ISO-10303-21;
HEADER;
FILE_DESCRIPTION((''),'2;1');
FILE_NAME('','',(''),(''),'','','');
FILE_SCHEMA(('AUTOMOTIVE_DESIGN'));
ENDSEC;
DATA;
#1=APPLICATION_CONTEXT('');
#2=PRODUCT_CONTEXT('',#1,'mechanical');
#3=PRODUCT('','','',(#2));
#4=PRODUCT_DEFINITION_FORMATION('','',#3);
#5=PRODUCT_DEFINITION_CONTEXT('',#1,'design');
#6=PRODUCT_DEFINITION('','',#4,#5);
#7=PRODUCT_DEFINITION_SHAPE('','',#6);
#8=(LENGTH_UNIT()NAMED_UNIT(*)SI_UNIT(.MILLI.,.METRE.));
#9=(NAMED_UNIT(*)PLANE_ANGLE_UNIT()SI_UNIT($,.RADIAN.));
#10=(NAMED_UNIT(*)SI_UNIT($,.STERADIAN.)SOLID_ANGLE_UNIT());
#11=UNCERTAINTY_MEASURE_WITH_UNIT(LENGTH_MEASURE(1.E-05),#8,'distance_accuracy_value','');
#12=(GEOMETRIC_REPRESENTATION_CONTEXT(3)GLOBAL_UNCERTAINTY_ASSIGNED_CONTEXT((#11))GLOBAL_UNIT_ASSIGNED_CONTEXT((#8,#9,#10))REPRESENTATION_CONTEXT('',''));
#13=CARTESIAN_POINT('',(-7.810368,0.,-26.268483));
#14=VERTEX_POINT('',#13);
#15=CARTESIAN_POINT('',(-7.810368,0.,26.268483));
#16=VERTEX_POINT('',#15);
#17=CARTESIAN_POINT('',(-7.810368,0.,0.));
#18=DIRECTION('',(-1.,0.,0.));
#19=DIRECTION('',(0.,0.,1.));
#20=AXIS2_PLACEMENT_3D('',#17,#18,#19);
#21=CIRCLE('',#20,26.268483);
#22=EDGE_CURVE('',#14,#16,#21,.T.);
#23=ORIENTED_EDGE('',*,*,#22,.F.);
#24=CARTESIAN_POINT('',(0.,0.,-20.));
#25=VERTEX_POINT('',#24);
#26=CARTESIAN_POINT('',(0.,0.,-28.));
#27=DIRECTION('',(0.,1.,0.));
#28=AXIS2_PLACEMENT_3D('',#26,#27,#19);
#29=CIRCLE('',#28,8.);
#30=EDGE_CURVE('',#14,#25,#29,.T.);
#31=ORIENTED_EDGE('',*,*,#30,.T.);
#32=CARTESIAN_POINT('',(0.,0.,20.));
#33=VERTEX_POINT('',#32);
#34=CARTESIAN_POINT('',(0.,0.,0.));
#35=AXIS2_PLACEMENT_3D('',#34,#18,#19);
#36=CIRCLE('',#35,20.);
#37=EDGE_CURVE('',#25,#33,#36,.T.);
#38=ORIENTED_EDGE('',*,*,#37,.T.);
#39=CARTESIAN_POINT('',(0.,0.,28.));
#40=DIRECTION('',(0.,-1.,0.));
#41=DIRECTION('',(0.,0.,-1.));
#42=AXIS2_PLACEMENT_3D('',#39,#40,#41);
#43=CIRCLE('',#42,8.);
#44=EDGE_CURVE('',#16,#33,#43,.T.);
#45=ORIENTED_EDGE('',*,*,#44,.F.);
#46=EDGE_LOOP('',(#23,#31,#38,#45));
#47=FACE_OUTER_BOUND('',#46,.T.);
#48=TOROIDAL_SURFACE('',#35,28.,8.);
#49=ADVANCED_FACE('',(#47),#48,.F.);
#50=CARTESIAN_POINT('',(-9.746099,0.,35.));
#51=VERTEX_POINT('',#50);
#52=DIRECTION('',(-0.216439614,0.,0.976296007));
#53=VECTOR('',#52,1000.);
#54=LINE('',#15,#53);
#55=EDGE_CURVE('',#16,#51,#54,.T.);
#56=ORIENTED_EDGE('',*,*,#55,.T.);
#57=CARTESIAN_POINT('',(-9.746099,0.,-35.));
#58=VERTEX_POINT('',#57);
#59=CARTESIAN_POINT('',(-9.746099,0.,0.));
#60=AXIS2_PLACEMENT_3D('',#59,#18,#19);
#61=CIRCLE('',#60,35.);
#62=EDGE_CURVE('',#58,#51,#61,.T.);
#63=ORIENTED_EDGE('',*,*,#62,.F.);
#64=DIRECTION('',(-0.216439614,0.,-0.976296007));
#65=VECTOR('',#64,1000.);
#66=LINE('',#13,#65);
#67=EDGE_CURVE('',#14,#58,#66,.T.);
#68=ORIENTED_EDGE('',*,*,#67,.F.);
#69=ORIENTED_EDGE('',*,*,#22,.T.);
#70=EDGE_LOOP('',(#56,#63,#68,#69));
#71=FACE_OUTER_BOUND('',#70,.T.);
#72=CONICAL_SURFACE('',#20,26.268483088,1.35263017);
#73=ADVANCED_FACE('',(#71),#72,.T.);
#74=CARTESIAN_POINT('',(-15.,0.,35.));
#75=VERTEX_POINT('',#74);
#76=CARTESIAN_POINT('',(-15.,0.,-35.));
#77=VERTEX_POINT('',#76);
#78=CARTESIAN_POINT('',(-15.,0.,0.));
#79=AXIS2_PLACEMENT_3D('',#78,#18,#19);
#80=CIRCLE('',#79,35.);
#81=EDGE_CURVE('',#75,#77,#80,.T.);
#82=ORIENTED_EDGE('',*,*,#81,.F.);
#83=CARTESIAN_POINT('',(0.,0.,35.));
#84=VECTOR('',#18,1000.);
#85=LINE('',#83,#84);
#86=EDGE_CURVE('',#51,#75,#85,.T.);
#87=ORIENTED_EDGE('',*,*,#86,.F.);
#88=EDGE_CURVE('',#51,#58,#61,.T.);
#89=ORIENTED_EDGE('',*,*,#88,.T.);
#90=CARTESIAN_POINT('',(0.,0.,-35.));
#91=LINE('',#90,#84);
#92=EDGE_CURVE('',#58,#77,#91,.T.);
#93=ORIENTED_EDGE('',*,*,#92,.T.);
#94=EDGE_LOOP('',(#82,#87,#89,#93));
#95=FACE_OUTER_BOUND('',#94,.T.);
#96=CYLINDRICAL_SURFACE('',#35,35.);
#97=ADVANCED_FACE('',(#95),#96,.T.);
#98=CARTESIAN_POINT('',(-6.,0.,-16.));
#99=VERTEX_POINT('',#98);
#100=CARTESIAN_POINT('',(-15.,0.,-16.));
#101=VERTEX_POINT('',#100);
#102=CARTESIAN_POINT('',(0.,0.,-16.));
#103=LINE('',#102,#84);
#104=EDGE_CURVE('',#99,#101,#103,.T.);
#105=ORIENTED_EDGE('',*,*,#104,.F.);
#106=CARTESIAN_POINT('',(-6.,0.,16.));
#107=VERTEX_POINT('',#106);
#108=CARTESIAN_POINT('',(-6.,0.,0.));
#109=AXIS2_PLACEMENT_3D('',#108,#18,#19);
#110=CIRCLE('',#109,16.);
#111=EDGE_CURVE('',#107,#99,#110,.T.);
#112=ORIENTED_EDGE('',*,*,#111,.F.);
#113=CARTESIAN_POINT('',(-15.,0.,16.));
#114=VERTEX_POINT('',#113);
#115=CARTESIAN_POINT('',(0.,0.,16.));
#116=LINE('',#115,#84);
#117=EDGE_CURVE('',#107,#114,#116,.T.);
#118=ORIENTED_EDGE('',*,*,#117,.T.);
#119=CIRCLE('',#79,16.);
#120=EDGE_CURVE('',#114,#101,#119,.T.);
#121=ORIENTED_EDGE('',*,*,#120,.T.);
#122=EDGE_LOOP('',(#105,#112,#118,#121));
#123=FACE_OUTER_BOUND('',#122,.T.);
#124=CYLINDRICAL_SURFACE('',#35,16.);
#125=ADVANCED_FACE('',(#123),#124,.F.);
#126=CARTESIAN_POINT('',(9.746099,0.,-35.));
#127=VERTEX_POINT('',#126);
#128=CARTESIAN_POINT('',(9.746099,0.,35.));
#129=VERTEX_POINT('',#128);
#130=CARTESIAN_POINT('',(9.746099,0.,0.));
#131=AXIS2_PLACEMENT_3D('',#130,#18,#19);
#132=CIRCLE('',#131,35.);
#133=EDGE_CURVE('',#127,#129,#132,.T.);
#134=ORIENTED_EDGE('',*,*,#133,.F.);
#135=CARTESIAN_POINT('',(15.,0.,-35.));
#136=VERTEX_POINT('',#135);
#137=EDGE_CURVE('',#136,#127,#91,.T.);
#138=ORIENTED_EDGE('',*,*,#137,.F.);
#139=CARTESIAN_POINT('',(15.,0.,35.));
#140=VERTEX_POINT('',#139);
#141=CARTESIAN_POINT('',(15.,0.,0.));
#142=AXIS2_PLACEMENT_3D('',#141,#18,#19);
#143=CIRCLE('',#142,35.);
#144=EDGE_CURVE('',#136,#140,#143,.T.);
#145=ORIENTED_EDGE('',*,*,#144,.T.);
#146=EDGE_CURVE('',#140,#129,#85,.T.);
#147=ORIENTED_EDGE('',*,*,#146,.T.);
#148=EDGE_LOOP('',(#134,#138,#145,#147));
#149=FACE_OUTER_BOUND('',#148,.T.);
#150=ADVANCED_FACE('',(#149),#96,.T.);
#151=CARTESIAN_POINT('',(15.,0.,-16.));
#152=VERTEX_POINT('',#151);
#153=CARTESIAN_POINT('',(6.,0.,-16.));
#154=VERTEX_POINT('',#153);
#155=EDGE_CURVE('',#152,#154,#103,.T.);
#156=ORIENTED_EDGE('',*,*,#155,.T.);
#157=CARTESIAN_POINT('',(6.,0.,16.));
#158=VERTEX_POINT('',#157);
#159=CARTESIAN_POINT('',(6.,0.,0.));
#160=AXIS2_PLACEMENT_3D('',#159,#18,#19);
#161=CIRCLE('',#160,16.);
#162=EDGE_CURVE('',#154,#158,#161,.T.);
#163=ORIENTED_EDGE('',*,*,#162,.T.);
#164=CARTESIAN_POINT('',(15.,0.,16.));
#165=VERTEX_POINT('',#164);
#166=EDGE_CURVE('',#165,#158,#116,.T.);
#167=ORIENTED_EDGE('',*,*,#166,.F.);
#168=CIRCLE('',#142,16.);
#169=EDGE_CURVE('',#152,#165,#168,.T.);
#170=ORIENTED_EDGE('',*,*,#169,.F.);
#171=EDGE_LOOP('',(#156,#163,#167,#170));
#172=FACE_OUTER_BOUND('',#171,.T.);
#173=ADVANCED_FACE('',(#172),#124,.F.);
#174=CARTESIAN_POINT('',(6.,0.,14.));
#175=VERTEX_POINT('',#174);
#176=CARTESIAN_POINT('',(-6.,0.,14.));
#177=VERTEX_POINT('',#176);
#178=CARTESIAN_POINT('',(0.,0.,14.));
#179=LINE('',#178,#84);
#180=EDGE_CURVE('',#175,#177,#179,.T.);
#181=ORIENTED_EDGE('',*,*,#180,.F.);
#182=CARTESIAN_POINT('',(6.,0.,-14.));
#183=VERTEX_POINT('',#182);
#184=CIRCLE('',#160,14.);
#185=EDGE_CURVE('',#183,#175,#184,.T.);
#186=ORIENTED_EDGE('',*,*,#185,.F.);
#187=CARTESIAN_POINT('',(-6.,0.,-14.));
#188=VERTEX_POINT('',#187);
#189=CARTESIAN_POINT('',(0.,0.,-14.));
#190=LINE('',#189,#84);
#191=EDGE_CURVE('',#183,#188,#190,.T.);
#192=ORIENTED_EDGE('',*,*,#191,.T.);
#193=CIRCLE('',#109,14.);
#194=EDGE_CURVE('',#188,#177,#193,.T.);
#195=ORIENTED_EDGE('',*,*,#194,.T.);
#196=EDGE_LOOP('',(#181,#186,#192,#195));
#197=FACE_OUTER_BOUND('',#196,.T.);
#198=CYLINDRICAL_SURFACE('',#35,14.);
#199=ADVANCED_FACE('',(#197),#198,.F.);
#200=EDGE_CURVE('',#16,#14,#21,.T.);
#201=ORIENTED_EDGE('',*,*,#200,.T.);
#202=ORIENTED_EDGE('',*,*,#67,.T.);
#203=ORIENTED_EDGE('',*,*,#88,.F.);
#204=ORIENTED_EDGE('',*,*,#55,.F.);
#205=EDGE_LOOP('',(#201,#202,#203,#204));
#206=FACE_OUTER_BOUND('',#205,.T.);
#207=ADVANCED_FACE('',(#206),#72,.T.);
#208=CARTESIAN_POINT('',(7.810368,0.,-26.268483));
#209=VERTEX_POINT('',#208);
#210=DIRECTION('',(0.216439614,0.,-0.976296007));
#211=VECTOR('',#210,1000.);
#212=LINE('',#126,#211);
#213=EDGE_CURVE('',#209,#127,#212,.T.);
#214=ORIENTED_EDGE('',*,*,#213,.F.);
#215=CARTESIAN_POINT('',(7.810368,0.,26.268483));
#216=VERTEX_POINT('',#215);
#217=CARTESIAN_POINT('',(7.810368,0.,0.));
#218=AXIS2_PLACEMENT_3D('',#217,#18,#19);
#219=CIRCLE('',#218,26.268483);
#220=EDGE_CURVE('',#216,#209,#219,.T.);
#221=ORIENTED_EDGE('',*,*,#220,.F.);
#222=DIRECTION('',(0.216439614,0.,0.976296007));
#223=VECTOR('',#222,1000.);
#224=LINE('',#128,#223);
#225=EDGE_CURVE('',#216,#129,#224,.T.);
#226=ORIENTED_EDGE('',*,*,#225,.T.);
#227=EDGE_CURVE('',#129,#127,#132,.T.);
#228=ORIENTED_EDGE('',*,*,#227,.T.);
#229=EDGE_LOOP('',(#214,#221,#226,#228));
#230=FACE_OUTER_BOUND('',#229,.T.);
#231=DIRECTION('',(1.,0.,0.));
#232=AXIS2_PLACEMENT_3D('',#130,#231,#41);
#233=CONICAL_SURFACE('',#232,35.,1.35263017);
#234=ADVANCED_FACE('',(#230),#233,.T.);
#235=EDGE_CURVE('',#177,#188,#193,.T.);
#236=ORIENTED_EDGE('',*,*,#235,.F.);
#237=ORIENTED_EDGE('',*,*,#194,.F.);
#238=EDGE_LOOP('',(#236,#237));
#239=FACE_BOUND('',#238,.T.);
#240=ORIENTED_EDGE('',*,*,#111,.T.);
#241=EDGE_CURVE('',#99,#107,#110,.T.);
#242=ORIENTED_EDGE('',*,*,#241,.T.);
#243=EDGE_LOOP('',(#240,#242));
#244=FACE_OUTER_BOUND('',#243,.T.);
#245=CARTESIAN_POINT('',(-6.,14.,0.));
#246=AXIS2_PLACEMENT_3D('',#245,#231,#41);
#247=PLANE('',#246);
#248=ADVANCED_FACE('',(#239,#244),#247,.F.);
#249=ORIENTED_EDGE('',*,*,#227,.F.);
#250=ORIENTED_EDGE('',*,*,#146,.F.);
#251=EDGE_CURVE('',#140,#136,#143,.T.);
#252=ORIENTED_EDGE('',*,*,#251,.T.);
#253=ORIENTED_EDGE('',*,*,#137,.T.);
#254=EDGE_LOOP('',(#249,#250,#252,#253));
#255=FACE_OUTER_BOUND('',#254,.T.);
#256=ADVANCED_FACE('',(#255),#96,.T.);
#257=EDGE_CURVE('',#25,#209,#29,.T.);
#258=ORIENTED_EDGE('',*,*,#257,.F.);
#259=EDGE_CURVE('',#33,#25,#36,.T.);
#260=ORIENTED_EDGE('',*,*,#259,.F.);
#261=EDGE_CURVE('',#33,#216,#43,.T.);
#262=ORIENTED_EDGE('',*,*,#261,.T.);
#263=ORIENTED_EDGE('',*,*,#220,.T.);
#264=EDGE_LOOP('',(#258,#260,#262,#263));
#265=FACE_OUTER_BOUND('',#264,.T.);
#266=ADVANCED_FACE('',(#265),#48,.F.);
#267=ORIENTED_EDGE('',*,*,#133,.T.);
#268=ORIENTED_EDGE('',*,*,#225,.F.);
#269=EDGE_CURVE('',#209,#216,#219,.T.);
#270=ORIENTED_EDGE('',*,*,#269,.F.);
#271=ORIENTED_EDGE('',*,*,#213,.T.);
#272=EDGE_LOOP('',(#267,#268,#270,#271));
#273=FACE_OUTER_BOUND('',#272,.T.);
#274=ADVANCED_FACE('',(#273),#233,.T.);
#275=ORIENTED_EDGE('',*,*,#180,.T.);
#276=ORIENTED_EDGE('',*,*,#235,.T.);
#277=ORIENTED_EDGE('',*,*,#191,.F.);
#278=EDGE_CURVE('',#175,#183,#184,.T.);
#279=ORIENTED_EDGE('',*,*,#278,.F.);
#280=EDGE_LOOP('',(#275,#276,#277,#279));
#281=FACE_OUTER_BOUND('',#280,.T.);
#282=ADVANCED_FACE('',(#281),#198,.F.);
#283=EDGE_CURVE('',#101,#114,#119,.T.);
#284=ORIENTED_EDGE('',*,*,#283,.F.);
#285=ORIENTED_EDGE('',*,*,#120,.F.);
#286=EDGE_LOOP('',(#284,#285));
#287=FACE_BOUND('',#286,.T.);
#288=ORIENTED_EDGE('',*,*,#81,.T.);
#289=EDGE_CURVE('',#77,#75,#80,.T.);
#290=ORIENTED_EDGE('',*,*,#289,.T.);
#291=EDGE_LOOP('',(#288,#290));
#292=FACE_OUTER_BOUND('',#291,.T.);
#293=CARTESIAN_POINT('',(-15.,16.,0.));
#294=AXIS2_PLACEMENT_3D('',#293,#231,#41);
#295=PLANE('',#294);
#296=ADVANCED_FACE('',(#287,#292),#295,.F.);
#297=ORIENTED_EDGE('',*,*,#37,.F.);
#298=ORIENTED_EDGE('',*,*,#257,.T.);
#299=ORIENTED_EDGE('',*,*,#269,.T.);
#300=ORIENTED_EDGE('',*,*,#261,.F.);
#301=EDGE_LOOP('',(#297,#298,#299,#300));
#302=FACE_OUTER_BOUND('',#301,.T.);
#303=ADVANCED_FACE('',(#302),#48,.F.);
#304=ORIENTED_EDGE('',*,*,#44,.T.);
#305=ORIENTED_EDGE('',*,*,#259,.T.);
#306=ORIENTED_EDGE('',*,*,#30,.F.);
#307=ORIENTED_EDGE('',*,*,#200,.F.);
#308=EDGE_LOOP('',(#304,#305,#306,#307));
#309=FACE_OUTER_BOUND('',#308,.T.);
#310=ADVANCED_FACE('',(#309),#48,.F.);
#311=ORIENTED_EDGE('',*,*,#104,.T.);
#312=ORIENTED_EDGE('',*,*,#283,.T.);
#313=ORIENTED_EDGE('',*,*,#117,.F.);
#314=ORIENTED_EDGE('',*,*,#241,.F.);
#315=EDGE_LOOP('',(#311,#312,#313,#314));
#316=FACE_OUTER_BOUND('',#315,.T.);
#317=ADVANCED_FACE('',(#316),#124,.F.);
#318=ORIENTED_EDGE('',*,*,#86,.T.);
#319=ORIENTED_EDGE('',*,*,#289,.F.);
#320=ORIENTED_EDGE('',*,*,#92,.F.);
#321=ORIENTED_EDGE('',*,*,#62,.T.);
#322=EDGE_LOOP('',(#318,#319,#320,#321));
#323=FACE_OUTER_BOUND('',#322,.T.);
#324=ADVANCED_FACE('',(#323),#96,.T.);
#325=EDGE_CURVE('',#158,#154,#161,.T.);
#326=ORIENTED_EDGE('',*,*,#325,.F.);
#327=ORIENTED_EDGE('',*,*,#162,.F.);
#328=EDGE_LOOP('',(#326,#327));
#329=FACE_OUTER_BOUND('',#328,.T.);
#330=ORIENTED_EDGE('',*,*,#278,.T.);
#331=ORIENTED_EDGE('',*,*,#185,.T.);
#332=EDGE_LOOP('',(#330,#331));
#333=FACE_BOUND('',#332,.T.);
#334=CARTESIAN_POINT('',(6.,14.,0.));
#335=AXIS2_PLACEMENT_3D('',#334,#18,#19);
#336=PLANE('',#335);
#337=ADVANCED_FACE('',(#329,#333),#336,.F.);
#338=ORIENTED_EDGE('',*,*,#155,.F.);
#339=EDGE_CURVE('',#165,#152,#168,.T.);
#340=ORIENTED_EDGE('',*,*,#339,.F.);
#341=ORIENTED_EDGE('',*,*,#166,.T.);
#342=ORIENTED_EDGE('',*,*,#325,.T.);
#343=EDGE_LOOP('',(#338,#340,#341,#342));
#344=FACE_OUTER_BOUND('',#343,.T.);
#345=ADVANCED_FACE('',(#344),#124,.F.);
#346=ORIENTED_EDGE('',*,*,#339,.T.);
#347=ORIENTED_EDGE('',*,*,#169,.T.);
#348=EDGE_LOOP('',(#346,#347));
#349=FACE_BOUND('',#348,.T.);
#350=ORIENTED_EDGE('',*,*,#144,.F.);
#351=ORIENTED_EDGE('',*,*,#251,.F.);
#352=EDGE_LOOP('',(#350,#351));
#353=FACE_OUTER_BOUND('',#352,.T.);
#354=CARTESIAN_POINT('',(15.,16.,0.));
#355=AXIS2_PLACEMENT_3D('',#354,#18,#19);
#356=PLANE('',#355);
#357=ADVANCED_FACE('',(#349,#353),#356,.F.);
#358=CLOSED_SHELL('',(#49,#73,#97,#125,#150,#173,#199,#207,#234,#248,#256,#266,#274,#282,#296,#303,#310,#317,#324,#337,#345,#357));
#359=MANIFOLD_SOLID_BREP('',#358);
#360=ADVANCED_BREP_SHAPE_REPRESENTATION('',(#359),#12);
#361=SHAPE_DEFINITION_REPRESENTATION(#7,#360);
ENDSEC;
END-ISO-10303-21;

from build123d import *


with BuildPart() as part:
    # Sketch1 → Revolve1 (revolve)
    with BuildSketch(Plane.XY, mode=Mode.PRIVATE) as revolve1_sk:
        with BuildLine():
            Line((-6, 14), (6, 14))
            Line((6, 14), (6, 16))
            Line((6, 16), (15, 16))
            Line((15, 16), (15, 35))
            Line((15, 35), (9.746098753, 35))
            Line((9.746098753, 35), (7.810368057, 26.268483088))
            ThreePointArc((7.810368057, 26.268483088), (5.007387777, 21.760924135), (0, 20))
            ThreePointArc((0, 20), (-5.007387777, 21.760924135), (-7.810368057, 26.268483088))
            Line((-7.810368057, 26.268483088), (-9.746098753, 35))
            Line((-9.746098753, 35), (-15, 35))
            Line((-15, 35), (-15, 16))
            Line((-15, 16), (-6, 16))
            Line((-6, 16), (-6, 14))
        make_face()
    revolve(revolve1_sk.sketch.rotate(Axis((0, 0, 0), (1, 0, 0)), 90), axis=Axis((0, 0, 0), (1, 0, 0)))


solid = part.part
